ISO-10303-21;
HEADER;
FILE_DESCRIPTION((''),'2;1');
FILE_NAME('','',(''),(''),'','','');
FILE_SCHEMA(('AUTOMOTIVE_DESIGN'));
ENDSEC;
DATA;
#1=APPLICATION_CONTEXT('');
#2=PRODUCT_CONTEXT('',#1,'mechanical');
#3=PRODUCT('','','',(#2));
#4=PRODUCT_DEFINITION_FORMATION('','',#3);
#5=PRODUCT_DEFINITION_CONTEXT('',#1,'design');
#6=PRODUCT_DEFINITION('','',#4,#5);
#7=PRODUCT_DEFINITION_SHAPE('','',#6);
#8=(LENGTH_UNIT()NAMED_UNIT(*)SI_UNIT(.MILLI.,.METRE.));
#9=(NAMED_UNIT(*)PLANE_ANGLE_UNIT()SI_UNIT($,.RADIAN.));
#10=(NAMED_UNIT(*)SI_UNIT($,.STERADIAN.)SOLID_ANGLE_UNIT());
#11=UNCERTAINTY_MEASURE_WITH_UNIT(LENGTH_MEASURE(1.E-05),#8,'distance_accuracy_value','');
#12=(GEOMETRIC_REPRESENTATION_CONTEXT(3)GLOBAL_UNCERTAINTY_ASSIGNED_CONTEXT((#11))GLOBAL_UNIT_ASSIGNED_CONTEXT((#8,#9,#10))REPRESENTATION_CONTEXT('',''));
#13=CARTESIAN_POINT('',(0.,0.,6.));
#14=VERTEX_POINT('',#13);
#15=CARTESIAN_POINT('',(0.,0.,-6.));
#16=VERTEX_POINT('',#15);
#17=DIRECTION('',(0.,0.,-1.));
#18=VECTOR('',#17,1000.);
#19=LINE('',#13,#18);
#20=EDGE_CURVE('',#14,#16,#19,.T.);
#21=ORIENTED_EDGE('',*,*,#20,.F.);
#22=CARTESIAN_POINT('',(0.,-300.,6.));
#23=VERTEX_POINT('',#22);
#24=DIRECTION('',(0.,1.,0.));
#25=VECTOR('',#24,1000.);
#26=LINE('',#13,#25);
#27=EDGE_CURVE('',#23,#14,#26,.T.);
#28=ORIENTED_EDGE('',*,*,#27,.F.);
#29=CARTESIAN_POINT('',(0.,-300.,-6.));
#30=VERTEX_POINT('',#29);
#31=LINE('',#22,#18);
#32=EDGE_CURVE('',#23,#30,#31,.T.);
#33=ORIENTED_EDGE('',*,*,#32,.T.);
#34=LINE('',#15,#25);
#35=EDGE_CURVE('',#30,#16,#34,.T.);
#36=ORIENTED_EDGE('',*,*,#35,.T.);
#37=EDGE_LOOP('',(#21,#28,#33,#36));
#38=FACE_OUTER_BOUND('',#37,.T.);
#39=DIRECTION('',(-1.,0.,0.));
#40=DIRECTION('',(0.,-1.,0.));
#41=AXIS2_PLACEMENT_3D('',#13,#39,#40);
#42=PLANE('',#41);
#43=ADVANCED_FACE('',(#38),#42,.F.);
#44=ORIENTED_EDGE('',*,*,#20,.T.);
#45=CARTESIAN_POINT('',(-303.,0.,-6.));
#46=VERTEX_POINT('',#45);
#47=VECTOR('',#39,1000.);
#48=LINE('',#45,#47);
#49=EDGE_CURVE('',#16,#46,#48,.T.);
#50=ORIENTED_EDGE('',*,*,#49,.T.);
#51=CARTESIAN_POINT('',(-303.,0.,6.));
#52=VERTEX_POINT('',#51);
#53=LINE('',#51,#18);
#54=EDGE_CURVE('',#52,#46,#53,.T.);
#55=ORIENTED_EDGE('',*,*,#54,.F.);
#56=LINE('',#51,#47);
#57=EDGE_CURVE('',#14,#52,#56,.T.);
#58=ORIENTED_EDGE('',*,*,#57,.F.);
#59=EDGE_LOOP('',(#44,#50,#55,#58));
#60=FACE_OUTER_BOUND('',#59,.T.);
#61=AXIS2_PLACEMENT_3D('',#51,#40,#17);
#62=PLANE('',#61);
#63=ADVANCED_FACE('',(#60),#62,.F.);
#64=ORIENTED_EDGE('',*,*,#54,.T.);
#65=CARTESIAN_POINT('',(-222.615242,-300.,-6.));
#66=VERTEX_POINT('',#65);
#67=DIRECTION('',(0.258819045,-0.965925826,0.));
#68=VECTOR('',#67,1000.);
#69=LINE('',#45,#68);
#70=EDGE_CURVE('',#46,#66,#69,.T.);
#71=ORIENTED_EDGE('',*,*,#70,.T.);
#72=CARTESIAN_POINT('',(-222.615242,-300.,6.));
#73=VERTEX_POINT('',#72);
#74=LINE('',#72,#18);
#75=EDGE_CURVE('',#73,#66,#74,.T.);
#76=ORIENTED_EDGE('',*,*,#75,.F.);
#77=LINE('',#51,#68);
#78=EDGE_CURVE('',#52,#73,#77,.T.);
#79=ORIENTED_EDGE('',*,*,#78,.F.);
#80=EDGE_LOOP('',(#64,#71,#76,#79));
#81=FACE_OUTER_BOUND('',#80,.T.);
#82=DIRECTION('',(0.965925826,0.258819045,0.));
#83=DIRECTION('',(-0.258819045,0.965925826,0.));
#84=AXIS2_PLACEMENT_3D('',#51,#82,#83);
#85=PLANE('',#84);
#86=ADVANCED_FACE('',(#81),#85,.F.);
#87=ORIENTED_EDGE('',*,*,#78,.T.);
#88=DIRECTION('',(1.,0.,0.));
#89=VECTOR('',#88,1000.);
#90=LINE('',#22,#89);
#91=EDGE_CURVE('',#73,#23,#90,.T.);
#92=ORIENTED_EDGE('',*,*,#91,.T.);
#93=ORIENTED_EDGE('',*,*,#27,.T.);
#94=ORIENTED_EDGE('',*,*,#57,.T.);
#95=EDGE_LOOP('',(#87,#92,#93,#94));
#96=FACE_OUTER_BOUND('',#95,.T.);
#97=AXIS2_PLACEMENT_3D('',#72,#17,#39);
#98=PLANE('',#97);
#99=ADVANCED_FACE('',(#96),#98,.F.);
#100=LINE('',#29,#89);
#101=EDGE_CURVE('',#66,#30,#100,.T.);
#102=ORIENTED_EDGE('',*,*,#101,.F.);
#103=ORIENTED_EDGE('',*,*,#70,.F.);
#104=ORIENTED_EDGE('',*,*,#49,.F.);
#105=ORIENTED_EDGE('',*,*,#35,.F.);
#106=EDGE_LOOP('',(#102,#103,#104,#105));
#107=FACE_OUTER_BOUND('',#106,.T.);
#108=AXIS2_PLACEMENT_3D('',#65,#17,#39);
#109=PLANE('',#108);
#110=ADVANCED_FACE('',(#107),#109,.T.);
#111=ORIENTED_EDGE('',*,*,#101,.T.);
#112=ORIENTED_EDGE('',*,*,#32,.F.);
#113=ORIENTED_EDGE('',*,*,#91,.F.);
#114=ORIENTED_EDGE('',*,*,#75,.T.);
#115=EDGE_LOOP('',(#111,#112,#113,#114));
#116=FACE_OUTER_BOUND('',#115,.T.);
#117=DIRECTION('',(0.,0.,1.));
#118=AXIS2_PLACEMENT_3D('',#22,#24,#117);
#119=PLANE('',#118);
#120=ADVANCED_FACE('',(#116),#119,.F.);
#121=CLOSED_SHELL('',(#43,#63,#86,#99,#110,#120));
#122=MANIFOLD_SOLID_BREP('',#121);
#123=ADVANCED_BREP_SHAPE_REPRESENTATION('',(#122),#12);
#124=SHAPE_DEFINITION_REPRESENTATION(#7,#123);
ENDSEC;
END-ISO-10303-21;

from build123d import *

# Parameters (mm, degrees)
EXTRUDE1_DEPTH = 6


with BuildPart() as part:
    # Sketch1 → Extrude1 (new, symmetric)
    with BuildSketch(Plane.XY):
        Polygon((-303, 0), (0, 0), (0, -300), (-222.615242271, -300), align=None)
    extrude(amount=EXTRUDE1_DEPTH, both=True)


solid = part.part
